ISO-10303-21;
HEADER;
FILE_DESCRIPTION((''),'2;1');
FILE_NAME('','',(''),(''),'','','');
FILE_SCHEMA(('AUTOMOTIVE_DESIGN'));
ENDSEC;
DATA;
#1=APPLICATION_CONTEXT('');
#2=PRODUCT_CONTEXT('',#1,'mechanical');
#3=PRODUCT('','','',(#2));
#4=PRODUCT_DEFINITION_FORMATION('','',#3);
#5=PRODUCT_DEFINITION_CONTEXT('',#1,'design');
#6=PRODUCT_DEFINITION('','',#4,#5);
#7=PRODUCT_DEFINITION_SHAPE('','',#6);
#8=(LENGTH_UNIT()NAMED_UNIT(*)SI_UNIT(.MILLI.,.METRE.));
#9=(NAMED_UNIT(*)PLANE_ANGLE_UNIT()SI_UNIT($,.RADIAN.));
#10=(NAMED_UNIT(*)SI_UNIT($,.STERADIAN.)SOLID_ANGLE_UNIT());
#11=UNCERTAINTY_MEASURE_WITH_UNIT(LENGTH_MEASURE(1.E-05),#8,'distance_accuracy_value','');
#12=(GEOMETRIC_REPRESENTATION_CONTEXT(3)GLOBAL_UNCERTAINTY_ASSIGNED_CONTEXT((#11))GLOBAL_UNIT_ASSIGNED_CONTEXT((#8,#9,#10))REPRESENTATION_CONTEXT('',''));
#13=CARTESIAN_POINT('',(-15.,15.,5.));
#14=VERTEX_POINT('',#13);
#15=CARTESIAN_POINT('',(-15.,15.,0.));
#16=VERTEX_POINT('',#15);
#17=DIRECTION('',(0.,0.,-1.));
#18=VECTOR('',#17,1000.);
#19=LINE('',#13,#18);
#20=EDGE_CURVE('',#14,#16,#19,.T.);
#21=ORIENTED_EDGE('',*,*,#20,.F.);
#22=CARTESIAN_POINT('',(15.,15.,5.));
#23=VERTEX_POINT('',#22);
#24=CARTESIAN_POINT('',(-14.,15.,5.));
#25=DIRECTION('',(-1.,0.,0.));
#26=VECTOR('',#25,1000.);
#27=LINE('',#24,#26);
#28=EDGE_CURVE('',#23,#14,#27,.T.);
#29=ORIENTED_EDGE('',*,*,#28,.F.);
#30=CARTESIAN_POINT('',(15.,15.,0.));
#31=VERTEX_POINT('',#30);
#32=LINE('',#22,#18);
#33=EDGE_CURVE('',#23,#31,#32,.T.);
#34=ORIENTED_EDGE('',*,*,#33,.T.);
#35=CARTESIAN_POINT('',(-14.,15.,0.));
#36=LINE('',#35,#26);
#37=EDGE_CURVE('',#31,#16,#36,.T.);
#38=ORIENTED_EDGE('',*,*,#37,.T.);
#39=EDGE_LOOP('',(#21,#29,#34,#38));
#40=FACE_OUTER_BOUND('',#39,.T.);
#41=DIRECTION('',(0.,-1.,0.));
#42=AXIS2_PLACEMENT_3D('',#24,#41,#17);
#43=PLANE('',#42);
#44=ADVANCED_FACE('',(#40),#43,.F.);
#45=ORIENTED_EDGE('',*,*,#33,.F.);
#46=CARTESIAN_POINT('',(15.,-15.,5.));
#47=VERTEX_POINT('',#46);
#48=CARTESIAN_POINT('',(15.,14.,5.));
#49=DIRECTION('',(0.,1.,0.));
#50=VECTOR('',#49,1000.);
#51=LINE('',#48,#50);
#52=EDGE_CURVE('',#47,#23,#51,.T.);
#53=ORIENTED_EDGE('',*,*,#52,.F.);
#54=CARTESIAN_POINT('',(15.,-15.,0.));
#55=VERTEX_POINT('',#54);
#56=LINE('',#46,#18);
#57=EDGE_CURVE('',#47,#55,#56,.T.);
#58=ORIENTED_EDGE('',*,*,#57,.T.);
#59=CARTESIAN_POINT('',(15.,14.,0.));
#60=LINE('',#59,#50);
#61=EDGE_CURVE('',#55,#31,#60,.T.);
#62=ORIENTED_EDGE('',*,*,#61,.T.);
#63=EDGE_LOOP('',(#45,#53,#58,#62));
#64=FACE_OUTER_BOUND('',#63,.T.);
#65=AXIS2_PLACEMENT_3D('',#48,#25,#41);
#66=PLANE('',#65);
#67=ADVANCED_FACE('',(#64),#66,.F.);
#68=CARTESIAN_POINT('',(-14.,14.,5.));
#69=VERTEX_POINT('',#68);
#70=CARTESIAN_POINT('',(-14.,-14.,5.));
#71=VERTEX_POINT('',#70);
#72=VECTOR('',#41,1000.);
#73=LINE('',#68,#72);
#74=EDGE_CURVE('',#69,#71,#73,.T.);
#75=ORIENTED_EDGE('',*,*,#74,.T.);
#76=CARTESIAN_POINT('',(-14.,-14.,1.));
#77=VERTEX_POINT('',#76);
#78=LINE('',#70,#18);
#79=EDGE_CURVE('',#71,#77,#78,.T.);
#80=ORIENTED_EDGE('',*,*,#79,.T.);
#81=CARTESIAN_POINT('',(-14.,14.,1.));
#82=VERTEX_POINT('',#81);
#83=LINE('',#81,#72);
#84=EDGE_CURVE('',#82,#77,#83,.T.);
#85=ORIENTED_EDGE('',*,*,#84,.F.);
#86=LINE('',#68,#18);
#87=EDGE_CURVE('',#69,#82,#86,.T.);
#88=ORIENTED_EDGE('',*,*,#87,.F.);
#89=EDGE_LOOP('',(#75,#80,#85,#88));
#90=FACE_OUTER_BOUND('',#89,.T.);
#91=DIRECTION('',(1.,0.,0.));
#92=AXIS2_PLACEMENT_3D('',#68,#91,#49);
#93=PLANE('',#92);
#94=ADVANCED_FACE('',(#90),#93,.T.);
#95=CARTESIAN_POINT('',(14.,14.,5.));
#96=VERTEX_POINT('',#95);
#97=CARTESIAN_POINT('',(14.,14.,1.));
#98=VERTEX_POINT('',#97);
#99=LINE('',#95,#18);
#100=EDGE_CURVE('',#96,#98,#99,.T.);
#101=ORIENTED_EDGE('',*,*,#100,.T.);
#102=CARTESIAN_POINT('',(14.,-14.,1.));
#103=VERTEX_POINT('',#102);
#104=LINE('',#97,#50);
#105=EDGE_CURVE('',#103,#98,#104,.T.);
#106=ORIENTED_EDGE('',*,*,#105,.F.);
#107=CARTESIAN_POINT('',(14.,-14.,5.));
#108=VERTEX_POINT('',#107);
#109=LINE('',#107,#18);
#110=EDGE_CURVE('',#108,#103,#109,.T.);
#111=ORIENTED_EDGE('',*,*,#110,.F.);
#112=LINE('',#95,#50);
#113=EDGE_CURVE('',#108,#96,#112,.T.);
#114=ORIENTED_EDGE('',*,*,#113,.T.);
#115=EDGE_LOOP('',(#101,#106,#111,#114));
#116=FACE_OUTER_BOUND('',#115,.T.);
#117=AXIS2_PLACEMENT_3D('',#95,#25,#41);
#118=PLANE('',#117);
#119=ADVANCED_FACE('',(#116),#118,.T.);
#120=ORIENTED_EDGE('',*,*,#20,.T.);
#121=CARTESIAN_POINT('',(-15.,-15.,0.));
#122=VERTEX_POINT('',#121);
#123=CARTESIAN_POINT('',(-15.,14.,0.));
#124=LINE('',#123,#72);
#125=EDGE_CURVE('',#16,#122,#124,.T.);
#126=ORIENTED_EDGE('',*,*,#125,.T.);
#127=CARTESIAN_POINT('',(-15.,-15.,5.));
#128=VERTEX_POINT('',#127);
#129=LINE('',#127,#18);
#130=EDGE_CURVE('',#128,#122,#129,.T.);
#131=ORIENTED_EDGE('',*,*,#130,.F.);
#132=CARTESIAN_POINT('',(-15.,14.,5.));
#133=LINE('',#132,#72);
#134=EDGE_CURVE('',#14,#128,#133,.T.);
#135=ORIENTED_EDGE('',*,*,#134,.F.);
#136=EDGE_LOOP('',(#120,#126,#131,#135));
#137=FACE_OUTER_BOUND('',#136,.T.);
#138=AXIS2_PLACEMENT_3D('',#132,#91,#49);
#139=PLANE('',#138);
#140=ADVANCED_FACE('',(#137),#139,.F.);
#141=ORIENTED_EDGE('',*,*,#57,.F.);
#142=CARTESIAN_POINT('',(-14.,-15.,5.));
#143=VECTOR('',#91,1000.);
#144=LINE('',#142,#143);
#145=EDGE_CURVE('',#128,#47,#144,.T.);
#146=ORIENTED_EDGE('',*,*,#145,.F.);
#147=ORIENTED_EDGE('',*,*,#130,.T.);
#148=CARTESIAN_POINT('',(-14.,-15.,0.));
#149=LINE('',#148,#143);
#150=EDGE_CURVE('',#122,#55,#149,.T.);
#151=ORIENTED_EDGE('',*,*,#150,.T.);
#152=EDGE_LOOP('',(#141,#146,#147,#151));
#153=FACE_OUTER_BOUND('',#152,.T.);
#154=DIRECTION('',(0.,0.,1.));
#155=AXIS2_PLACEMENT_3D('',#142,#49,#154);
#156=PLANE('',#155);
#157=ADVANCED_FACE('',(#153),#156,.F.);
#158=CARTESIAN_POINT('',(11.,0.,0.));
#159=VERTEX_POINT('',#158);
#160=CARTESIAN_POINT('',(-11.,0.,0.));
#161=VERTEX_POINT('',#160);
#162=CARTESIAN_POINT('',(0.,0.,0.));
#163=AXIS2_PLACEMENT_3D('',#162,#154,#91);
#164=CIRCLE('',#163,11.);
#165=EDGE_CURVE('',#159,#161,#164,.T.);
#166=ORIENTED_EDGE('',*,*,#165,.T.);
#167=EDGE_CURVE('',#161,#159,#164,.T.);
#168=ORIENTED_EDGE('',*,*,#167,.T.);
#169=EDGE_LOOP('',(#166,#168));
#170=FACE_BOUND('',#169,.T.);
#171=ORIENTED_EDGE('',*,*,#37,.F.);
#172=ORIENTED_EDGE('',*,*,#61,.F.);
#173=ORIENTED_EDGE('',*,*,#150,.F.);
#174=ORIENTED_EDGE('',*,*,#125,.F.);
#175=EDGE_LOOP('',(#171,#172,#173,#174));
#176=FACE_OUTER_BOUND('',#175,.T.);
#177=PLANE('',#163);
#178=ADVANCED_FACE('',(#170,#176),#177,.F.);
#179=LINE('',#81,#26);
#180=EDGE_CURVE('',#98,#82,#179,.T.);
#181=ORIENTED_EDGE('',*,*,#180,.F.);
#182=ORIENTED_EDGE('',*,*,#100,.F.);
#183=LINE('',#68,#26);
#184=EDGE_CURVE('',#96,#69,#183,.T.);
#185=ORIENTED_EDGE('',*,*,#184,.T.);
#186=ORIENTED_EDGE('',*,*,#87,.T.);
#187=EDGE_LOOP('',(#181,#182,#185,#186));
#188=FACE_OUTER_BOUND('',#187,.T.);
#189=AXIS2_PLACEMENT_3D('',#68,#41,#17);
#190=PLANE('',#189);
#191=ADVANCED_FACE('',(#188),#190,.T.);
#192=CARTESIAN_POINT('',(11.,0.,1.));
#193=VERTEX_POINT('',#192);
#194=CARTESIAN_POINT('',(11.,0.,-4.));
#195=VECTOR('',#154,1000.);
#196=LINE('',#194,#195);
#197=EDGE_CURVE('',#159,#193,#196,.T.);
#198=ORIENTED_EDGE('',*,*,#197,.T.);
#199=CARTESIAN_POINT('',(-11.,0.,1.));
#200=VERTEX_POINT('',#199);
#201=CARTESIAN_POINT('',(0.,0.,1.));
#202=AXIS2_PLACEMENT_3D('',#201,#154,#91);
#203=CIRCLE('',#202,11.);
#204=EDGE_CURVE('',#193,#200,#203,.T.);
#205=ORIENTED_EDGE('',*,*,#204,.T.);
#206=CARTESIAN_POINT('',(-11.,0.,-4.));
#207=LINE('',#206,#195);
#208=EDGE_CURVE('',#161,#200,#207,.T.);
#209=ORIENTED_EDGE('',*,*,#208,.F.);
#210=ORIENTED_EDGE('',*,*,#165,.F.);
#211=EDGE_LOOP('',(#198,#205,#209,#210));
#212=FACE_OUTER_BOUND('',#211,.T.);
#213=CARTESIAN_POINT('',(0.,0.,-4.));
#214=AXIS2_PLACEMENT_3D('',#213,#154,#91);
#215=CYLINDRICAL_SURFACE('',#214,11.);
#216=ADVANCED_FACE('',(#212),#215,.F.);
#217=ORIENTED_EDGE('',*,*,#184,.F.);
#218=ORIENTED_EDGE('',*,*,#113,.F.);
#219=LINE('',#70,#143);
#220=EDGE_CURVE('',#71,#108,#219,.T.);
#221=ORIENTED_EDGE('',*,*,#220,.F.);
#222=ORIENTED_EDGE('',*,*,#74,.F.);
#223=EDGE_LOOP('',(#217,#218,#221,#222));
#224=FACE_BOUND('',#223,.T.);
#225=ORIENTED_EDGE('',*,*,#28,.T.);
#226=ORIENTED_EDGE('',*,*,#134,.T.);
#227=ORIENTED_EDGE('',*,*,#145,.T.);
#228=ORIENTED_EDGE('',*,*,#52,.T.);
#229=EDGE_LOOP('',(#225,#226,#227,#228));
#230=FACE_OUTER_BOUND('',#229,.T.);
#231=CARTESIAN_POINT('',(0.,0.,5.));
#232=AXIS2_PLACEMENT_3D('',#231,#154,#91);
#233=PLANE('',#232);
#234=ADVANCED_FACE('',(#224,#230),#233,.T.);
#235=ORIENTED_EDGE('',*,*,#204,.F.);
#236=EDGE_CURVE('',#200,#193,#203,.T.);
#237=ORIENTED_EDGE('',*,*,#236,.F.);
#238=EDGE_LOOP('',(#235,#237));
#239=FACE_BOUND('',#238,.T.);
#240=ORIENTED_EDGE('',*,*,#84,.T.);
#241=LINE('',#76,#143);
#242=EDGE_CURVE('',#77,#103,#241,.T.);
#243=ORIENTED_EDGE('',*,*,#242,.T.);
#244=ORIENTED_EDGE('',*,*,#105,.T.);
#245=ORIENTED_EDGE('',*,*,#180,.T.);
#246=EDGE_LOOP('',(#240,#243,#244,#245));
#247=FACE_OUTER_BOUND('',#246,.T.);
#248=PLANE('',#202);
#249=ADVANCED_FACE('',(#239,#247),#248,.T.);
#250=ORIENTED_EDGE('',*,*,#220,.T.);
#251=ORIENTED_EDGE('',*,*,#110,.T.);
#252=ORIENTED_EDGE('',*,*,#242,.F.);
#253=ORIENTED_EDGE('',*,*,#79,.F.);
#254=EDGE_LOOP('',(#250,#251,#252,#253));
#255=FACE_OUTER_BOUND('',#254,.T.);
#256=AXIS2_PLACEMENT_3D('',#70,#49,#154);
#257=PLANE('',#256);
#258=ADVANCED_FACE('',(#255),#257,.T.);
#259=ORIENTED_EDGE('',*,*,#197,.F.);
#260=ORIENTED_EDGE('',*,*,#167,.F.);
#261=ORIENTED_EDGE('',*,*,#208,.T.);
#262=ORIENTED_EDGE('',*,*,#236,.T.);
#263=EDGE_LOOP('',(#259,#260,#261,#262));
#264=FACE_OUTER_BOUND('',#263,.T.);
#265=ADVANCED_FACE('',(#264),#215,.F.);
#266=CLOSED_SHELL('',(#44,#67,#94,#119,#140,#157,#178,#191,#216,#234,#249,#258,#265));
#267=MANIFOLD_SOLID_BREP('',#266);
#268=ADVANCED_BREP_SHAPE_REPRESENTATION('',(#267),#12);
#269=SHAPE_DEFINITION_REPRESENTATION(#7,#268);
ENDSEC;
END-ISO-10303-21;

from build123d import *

# Parameters (mm, degrees)
SKETCH_1_3_W        = 28
SKETCH_1_3_H        = 28
BOSS_EXTRUDE1_DEPTH = 1
SKETCH_1_3_2_W      = 30
SKETCH_1_3_2_H      = 30
SKETCH_1_3_2_W_2    = 28
SKETCH_1_3_2_H_2    = 28
EXTRUDE_THIN1_DEPTH = 5
SKETCH2_R           = 11
CUT_EXTRUDE1_DEPTH  = 5


with BuildPart() as part:
    # Sketch 1_3 → Boss-Extrude1 (new body)
    with BuildSketch(Plane.XY):
        Rectangle(SKETCH_1_3_W, SKETCH_1_3_H)
    extrude(amount=BOSS_EXTRUDE1_DEPTH)

    # Sketch 1_3 2 → Extrude-Thin1 (add)
    with BuildSketch(Plane.XY):
        Rectangle(SKETCH_1_3_2_W, SKETCH_1_3_2_H)
        Rectangle(SKETCH_1_3_2_W_2, SKETCH_1_3_2_H_2, mode=Mode.SUBTRACT)
    extrude(amount=EXTRUDE_THIN1_DEPTH)

    # Sketch2 → Cut-Extrude1 (cut)
    with BuildSketch(Plane.XY.offset(1)):
        Circle(SKETCH2_R)
    extrude(amount=-CUT_EXTRUDE1_DEPTH, mode=Mode.SUBTRACT)


solid = part.part
